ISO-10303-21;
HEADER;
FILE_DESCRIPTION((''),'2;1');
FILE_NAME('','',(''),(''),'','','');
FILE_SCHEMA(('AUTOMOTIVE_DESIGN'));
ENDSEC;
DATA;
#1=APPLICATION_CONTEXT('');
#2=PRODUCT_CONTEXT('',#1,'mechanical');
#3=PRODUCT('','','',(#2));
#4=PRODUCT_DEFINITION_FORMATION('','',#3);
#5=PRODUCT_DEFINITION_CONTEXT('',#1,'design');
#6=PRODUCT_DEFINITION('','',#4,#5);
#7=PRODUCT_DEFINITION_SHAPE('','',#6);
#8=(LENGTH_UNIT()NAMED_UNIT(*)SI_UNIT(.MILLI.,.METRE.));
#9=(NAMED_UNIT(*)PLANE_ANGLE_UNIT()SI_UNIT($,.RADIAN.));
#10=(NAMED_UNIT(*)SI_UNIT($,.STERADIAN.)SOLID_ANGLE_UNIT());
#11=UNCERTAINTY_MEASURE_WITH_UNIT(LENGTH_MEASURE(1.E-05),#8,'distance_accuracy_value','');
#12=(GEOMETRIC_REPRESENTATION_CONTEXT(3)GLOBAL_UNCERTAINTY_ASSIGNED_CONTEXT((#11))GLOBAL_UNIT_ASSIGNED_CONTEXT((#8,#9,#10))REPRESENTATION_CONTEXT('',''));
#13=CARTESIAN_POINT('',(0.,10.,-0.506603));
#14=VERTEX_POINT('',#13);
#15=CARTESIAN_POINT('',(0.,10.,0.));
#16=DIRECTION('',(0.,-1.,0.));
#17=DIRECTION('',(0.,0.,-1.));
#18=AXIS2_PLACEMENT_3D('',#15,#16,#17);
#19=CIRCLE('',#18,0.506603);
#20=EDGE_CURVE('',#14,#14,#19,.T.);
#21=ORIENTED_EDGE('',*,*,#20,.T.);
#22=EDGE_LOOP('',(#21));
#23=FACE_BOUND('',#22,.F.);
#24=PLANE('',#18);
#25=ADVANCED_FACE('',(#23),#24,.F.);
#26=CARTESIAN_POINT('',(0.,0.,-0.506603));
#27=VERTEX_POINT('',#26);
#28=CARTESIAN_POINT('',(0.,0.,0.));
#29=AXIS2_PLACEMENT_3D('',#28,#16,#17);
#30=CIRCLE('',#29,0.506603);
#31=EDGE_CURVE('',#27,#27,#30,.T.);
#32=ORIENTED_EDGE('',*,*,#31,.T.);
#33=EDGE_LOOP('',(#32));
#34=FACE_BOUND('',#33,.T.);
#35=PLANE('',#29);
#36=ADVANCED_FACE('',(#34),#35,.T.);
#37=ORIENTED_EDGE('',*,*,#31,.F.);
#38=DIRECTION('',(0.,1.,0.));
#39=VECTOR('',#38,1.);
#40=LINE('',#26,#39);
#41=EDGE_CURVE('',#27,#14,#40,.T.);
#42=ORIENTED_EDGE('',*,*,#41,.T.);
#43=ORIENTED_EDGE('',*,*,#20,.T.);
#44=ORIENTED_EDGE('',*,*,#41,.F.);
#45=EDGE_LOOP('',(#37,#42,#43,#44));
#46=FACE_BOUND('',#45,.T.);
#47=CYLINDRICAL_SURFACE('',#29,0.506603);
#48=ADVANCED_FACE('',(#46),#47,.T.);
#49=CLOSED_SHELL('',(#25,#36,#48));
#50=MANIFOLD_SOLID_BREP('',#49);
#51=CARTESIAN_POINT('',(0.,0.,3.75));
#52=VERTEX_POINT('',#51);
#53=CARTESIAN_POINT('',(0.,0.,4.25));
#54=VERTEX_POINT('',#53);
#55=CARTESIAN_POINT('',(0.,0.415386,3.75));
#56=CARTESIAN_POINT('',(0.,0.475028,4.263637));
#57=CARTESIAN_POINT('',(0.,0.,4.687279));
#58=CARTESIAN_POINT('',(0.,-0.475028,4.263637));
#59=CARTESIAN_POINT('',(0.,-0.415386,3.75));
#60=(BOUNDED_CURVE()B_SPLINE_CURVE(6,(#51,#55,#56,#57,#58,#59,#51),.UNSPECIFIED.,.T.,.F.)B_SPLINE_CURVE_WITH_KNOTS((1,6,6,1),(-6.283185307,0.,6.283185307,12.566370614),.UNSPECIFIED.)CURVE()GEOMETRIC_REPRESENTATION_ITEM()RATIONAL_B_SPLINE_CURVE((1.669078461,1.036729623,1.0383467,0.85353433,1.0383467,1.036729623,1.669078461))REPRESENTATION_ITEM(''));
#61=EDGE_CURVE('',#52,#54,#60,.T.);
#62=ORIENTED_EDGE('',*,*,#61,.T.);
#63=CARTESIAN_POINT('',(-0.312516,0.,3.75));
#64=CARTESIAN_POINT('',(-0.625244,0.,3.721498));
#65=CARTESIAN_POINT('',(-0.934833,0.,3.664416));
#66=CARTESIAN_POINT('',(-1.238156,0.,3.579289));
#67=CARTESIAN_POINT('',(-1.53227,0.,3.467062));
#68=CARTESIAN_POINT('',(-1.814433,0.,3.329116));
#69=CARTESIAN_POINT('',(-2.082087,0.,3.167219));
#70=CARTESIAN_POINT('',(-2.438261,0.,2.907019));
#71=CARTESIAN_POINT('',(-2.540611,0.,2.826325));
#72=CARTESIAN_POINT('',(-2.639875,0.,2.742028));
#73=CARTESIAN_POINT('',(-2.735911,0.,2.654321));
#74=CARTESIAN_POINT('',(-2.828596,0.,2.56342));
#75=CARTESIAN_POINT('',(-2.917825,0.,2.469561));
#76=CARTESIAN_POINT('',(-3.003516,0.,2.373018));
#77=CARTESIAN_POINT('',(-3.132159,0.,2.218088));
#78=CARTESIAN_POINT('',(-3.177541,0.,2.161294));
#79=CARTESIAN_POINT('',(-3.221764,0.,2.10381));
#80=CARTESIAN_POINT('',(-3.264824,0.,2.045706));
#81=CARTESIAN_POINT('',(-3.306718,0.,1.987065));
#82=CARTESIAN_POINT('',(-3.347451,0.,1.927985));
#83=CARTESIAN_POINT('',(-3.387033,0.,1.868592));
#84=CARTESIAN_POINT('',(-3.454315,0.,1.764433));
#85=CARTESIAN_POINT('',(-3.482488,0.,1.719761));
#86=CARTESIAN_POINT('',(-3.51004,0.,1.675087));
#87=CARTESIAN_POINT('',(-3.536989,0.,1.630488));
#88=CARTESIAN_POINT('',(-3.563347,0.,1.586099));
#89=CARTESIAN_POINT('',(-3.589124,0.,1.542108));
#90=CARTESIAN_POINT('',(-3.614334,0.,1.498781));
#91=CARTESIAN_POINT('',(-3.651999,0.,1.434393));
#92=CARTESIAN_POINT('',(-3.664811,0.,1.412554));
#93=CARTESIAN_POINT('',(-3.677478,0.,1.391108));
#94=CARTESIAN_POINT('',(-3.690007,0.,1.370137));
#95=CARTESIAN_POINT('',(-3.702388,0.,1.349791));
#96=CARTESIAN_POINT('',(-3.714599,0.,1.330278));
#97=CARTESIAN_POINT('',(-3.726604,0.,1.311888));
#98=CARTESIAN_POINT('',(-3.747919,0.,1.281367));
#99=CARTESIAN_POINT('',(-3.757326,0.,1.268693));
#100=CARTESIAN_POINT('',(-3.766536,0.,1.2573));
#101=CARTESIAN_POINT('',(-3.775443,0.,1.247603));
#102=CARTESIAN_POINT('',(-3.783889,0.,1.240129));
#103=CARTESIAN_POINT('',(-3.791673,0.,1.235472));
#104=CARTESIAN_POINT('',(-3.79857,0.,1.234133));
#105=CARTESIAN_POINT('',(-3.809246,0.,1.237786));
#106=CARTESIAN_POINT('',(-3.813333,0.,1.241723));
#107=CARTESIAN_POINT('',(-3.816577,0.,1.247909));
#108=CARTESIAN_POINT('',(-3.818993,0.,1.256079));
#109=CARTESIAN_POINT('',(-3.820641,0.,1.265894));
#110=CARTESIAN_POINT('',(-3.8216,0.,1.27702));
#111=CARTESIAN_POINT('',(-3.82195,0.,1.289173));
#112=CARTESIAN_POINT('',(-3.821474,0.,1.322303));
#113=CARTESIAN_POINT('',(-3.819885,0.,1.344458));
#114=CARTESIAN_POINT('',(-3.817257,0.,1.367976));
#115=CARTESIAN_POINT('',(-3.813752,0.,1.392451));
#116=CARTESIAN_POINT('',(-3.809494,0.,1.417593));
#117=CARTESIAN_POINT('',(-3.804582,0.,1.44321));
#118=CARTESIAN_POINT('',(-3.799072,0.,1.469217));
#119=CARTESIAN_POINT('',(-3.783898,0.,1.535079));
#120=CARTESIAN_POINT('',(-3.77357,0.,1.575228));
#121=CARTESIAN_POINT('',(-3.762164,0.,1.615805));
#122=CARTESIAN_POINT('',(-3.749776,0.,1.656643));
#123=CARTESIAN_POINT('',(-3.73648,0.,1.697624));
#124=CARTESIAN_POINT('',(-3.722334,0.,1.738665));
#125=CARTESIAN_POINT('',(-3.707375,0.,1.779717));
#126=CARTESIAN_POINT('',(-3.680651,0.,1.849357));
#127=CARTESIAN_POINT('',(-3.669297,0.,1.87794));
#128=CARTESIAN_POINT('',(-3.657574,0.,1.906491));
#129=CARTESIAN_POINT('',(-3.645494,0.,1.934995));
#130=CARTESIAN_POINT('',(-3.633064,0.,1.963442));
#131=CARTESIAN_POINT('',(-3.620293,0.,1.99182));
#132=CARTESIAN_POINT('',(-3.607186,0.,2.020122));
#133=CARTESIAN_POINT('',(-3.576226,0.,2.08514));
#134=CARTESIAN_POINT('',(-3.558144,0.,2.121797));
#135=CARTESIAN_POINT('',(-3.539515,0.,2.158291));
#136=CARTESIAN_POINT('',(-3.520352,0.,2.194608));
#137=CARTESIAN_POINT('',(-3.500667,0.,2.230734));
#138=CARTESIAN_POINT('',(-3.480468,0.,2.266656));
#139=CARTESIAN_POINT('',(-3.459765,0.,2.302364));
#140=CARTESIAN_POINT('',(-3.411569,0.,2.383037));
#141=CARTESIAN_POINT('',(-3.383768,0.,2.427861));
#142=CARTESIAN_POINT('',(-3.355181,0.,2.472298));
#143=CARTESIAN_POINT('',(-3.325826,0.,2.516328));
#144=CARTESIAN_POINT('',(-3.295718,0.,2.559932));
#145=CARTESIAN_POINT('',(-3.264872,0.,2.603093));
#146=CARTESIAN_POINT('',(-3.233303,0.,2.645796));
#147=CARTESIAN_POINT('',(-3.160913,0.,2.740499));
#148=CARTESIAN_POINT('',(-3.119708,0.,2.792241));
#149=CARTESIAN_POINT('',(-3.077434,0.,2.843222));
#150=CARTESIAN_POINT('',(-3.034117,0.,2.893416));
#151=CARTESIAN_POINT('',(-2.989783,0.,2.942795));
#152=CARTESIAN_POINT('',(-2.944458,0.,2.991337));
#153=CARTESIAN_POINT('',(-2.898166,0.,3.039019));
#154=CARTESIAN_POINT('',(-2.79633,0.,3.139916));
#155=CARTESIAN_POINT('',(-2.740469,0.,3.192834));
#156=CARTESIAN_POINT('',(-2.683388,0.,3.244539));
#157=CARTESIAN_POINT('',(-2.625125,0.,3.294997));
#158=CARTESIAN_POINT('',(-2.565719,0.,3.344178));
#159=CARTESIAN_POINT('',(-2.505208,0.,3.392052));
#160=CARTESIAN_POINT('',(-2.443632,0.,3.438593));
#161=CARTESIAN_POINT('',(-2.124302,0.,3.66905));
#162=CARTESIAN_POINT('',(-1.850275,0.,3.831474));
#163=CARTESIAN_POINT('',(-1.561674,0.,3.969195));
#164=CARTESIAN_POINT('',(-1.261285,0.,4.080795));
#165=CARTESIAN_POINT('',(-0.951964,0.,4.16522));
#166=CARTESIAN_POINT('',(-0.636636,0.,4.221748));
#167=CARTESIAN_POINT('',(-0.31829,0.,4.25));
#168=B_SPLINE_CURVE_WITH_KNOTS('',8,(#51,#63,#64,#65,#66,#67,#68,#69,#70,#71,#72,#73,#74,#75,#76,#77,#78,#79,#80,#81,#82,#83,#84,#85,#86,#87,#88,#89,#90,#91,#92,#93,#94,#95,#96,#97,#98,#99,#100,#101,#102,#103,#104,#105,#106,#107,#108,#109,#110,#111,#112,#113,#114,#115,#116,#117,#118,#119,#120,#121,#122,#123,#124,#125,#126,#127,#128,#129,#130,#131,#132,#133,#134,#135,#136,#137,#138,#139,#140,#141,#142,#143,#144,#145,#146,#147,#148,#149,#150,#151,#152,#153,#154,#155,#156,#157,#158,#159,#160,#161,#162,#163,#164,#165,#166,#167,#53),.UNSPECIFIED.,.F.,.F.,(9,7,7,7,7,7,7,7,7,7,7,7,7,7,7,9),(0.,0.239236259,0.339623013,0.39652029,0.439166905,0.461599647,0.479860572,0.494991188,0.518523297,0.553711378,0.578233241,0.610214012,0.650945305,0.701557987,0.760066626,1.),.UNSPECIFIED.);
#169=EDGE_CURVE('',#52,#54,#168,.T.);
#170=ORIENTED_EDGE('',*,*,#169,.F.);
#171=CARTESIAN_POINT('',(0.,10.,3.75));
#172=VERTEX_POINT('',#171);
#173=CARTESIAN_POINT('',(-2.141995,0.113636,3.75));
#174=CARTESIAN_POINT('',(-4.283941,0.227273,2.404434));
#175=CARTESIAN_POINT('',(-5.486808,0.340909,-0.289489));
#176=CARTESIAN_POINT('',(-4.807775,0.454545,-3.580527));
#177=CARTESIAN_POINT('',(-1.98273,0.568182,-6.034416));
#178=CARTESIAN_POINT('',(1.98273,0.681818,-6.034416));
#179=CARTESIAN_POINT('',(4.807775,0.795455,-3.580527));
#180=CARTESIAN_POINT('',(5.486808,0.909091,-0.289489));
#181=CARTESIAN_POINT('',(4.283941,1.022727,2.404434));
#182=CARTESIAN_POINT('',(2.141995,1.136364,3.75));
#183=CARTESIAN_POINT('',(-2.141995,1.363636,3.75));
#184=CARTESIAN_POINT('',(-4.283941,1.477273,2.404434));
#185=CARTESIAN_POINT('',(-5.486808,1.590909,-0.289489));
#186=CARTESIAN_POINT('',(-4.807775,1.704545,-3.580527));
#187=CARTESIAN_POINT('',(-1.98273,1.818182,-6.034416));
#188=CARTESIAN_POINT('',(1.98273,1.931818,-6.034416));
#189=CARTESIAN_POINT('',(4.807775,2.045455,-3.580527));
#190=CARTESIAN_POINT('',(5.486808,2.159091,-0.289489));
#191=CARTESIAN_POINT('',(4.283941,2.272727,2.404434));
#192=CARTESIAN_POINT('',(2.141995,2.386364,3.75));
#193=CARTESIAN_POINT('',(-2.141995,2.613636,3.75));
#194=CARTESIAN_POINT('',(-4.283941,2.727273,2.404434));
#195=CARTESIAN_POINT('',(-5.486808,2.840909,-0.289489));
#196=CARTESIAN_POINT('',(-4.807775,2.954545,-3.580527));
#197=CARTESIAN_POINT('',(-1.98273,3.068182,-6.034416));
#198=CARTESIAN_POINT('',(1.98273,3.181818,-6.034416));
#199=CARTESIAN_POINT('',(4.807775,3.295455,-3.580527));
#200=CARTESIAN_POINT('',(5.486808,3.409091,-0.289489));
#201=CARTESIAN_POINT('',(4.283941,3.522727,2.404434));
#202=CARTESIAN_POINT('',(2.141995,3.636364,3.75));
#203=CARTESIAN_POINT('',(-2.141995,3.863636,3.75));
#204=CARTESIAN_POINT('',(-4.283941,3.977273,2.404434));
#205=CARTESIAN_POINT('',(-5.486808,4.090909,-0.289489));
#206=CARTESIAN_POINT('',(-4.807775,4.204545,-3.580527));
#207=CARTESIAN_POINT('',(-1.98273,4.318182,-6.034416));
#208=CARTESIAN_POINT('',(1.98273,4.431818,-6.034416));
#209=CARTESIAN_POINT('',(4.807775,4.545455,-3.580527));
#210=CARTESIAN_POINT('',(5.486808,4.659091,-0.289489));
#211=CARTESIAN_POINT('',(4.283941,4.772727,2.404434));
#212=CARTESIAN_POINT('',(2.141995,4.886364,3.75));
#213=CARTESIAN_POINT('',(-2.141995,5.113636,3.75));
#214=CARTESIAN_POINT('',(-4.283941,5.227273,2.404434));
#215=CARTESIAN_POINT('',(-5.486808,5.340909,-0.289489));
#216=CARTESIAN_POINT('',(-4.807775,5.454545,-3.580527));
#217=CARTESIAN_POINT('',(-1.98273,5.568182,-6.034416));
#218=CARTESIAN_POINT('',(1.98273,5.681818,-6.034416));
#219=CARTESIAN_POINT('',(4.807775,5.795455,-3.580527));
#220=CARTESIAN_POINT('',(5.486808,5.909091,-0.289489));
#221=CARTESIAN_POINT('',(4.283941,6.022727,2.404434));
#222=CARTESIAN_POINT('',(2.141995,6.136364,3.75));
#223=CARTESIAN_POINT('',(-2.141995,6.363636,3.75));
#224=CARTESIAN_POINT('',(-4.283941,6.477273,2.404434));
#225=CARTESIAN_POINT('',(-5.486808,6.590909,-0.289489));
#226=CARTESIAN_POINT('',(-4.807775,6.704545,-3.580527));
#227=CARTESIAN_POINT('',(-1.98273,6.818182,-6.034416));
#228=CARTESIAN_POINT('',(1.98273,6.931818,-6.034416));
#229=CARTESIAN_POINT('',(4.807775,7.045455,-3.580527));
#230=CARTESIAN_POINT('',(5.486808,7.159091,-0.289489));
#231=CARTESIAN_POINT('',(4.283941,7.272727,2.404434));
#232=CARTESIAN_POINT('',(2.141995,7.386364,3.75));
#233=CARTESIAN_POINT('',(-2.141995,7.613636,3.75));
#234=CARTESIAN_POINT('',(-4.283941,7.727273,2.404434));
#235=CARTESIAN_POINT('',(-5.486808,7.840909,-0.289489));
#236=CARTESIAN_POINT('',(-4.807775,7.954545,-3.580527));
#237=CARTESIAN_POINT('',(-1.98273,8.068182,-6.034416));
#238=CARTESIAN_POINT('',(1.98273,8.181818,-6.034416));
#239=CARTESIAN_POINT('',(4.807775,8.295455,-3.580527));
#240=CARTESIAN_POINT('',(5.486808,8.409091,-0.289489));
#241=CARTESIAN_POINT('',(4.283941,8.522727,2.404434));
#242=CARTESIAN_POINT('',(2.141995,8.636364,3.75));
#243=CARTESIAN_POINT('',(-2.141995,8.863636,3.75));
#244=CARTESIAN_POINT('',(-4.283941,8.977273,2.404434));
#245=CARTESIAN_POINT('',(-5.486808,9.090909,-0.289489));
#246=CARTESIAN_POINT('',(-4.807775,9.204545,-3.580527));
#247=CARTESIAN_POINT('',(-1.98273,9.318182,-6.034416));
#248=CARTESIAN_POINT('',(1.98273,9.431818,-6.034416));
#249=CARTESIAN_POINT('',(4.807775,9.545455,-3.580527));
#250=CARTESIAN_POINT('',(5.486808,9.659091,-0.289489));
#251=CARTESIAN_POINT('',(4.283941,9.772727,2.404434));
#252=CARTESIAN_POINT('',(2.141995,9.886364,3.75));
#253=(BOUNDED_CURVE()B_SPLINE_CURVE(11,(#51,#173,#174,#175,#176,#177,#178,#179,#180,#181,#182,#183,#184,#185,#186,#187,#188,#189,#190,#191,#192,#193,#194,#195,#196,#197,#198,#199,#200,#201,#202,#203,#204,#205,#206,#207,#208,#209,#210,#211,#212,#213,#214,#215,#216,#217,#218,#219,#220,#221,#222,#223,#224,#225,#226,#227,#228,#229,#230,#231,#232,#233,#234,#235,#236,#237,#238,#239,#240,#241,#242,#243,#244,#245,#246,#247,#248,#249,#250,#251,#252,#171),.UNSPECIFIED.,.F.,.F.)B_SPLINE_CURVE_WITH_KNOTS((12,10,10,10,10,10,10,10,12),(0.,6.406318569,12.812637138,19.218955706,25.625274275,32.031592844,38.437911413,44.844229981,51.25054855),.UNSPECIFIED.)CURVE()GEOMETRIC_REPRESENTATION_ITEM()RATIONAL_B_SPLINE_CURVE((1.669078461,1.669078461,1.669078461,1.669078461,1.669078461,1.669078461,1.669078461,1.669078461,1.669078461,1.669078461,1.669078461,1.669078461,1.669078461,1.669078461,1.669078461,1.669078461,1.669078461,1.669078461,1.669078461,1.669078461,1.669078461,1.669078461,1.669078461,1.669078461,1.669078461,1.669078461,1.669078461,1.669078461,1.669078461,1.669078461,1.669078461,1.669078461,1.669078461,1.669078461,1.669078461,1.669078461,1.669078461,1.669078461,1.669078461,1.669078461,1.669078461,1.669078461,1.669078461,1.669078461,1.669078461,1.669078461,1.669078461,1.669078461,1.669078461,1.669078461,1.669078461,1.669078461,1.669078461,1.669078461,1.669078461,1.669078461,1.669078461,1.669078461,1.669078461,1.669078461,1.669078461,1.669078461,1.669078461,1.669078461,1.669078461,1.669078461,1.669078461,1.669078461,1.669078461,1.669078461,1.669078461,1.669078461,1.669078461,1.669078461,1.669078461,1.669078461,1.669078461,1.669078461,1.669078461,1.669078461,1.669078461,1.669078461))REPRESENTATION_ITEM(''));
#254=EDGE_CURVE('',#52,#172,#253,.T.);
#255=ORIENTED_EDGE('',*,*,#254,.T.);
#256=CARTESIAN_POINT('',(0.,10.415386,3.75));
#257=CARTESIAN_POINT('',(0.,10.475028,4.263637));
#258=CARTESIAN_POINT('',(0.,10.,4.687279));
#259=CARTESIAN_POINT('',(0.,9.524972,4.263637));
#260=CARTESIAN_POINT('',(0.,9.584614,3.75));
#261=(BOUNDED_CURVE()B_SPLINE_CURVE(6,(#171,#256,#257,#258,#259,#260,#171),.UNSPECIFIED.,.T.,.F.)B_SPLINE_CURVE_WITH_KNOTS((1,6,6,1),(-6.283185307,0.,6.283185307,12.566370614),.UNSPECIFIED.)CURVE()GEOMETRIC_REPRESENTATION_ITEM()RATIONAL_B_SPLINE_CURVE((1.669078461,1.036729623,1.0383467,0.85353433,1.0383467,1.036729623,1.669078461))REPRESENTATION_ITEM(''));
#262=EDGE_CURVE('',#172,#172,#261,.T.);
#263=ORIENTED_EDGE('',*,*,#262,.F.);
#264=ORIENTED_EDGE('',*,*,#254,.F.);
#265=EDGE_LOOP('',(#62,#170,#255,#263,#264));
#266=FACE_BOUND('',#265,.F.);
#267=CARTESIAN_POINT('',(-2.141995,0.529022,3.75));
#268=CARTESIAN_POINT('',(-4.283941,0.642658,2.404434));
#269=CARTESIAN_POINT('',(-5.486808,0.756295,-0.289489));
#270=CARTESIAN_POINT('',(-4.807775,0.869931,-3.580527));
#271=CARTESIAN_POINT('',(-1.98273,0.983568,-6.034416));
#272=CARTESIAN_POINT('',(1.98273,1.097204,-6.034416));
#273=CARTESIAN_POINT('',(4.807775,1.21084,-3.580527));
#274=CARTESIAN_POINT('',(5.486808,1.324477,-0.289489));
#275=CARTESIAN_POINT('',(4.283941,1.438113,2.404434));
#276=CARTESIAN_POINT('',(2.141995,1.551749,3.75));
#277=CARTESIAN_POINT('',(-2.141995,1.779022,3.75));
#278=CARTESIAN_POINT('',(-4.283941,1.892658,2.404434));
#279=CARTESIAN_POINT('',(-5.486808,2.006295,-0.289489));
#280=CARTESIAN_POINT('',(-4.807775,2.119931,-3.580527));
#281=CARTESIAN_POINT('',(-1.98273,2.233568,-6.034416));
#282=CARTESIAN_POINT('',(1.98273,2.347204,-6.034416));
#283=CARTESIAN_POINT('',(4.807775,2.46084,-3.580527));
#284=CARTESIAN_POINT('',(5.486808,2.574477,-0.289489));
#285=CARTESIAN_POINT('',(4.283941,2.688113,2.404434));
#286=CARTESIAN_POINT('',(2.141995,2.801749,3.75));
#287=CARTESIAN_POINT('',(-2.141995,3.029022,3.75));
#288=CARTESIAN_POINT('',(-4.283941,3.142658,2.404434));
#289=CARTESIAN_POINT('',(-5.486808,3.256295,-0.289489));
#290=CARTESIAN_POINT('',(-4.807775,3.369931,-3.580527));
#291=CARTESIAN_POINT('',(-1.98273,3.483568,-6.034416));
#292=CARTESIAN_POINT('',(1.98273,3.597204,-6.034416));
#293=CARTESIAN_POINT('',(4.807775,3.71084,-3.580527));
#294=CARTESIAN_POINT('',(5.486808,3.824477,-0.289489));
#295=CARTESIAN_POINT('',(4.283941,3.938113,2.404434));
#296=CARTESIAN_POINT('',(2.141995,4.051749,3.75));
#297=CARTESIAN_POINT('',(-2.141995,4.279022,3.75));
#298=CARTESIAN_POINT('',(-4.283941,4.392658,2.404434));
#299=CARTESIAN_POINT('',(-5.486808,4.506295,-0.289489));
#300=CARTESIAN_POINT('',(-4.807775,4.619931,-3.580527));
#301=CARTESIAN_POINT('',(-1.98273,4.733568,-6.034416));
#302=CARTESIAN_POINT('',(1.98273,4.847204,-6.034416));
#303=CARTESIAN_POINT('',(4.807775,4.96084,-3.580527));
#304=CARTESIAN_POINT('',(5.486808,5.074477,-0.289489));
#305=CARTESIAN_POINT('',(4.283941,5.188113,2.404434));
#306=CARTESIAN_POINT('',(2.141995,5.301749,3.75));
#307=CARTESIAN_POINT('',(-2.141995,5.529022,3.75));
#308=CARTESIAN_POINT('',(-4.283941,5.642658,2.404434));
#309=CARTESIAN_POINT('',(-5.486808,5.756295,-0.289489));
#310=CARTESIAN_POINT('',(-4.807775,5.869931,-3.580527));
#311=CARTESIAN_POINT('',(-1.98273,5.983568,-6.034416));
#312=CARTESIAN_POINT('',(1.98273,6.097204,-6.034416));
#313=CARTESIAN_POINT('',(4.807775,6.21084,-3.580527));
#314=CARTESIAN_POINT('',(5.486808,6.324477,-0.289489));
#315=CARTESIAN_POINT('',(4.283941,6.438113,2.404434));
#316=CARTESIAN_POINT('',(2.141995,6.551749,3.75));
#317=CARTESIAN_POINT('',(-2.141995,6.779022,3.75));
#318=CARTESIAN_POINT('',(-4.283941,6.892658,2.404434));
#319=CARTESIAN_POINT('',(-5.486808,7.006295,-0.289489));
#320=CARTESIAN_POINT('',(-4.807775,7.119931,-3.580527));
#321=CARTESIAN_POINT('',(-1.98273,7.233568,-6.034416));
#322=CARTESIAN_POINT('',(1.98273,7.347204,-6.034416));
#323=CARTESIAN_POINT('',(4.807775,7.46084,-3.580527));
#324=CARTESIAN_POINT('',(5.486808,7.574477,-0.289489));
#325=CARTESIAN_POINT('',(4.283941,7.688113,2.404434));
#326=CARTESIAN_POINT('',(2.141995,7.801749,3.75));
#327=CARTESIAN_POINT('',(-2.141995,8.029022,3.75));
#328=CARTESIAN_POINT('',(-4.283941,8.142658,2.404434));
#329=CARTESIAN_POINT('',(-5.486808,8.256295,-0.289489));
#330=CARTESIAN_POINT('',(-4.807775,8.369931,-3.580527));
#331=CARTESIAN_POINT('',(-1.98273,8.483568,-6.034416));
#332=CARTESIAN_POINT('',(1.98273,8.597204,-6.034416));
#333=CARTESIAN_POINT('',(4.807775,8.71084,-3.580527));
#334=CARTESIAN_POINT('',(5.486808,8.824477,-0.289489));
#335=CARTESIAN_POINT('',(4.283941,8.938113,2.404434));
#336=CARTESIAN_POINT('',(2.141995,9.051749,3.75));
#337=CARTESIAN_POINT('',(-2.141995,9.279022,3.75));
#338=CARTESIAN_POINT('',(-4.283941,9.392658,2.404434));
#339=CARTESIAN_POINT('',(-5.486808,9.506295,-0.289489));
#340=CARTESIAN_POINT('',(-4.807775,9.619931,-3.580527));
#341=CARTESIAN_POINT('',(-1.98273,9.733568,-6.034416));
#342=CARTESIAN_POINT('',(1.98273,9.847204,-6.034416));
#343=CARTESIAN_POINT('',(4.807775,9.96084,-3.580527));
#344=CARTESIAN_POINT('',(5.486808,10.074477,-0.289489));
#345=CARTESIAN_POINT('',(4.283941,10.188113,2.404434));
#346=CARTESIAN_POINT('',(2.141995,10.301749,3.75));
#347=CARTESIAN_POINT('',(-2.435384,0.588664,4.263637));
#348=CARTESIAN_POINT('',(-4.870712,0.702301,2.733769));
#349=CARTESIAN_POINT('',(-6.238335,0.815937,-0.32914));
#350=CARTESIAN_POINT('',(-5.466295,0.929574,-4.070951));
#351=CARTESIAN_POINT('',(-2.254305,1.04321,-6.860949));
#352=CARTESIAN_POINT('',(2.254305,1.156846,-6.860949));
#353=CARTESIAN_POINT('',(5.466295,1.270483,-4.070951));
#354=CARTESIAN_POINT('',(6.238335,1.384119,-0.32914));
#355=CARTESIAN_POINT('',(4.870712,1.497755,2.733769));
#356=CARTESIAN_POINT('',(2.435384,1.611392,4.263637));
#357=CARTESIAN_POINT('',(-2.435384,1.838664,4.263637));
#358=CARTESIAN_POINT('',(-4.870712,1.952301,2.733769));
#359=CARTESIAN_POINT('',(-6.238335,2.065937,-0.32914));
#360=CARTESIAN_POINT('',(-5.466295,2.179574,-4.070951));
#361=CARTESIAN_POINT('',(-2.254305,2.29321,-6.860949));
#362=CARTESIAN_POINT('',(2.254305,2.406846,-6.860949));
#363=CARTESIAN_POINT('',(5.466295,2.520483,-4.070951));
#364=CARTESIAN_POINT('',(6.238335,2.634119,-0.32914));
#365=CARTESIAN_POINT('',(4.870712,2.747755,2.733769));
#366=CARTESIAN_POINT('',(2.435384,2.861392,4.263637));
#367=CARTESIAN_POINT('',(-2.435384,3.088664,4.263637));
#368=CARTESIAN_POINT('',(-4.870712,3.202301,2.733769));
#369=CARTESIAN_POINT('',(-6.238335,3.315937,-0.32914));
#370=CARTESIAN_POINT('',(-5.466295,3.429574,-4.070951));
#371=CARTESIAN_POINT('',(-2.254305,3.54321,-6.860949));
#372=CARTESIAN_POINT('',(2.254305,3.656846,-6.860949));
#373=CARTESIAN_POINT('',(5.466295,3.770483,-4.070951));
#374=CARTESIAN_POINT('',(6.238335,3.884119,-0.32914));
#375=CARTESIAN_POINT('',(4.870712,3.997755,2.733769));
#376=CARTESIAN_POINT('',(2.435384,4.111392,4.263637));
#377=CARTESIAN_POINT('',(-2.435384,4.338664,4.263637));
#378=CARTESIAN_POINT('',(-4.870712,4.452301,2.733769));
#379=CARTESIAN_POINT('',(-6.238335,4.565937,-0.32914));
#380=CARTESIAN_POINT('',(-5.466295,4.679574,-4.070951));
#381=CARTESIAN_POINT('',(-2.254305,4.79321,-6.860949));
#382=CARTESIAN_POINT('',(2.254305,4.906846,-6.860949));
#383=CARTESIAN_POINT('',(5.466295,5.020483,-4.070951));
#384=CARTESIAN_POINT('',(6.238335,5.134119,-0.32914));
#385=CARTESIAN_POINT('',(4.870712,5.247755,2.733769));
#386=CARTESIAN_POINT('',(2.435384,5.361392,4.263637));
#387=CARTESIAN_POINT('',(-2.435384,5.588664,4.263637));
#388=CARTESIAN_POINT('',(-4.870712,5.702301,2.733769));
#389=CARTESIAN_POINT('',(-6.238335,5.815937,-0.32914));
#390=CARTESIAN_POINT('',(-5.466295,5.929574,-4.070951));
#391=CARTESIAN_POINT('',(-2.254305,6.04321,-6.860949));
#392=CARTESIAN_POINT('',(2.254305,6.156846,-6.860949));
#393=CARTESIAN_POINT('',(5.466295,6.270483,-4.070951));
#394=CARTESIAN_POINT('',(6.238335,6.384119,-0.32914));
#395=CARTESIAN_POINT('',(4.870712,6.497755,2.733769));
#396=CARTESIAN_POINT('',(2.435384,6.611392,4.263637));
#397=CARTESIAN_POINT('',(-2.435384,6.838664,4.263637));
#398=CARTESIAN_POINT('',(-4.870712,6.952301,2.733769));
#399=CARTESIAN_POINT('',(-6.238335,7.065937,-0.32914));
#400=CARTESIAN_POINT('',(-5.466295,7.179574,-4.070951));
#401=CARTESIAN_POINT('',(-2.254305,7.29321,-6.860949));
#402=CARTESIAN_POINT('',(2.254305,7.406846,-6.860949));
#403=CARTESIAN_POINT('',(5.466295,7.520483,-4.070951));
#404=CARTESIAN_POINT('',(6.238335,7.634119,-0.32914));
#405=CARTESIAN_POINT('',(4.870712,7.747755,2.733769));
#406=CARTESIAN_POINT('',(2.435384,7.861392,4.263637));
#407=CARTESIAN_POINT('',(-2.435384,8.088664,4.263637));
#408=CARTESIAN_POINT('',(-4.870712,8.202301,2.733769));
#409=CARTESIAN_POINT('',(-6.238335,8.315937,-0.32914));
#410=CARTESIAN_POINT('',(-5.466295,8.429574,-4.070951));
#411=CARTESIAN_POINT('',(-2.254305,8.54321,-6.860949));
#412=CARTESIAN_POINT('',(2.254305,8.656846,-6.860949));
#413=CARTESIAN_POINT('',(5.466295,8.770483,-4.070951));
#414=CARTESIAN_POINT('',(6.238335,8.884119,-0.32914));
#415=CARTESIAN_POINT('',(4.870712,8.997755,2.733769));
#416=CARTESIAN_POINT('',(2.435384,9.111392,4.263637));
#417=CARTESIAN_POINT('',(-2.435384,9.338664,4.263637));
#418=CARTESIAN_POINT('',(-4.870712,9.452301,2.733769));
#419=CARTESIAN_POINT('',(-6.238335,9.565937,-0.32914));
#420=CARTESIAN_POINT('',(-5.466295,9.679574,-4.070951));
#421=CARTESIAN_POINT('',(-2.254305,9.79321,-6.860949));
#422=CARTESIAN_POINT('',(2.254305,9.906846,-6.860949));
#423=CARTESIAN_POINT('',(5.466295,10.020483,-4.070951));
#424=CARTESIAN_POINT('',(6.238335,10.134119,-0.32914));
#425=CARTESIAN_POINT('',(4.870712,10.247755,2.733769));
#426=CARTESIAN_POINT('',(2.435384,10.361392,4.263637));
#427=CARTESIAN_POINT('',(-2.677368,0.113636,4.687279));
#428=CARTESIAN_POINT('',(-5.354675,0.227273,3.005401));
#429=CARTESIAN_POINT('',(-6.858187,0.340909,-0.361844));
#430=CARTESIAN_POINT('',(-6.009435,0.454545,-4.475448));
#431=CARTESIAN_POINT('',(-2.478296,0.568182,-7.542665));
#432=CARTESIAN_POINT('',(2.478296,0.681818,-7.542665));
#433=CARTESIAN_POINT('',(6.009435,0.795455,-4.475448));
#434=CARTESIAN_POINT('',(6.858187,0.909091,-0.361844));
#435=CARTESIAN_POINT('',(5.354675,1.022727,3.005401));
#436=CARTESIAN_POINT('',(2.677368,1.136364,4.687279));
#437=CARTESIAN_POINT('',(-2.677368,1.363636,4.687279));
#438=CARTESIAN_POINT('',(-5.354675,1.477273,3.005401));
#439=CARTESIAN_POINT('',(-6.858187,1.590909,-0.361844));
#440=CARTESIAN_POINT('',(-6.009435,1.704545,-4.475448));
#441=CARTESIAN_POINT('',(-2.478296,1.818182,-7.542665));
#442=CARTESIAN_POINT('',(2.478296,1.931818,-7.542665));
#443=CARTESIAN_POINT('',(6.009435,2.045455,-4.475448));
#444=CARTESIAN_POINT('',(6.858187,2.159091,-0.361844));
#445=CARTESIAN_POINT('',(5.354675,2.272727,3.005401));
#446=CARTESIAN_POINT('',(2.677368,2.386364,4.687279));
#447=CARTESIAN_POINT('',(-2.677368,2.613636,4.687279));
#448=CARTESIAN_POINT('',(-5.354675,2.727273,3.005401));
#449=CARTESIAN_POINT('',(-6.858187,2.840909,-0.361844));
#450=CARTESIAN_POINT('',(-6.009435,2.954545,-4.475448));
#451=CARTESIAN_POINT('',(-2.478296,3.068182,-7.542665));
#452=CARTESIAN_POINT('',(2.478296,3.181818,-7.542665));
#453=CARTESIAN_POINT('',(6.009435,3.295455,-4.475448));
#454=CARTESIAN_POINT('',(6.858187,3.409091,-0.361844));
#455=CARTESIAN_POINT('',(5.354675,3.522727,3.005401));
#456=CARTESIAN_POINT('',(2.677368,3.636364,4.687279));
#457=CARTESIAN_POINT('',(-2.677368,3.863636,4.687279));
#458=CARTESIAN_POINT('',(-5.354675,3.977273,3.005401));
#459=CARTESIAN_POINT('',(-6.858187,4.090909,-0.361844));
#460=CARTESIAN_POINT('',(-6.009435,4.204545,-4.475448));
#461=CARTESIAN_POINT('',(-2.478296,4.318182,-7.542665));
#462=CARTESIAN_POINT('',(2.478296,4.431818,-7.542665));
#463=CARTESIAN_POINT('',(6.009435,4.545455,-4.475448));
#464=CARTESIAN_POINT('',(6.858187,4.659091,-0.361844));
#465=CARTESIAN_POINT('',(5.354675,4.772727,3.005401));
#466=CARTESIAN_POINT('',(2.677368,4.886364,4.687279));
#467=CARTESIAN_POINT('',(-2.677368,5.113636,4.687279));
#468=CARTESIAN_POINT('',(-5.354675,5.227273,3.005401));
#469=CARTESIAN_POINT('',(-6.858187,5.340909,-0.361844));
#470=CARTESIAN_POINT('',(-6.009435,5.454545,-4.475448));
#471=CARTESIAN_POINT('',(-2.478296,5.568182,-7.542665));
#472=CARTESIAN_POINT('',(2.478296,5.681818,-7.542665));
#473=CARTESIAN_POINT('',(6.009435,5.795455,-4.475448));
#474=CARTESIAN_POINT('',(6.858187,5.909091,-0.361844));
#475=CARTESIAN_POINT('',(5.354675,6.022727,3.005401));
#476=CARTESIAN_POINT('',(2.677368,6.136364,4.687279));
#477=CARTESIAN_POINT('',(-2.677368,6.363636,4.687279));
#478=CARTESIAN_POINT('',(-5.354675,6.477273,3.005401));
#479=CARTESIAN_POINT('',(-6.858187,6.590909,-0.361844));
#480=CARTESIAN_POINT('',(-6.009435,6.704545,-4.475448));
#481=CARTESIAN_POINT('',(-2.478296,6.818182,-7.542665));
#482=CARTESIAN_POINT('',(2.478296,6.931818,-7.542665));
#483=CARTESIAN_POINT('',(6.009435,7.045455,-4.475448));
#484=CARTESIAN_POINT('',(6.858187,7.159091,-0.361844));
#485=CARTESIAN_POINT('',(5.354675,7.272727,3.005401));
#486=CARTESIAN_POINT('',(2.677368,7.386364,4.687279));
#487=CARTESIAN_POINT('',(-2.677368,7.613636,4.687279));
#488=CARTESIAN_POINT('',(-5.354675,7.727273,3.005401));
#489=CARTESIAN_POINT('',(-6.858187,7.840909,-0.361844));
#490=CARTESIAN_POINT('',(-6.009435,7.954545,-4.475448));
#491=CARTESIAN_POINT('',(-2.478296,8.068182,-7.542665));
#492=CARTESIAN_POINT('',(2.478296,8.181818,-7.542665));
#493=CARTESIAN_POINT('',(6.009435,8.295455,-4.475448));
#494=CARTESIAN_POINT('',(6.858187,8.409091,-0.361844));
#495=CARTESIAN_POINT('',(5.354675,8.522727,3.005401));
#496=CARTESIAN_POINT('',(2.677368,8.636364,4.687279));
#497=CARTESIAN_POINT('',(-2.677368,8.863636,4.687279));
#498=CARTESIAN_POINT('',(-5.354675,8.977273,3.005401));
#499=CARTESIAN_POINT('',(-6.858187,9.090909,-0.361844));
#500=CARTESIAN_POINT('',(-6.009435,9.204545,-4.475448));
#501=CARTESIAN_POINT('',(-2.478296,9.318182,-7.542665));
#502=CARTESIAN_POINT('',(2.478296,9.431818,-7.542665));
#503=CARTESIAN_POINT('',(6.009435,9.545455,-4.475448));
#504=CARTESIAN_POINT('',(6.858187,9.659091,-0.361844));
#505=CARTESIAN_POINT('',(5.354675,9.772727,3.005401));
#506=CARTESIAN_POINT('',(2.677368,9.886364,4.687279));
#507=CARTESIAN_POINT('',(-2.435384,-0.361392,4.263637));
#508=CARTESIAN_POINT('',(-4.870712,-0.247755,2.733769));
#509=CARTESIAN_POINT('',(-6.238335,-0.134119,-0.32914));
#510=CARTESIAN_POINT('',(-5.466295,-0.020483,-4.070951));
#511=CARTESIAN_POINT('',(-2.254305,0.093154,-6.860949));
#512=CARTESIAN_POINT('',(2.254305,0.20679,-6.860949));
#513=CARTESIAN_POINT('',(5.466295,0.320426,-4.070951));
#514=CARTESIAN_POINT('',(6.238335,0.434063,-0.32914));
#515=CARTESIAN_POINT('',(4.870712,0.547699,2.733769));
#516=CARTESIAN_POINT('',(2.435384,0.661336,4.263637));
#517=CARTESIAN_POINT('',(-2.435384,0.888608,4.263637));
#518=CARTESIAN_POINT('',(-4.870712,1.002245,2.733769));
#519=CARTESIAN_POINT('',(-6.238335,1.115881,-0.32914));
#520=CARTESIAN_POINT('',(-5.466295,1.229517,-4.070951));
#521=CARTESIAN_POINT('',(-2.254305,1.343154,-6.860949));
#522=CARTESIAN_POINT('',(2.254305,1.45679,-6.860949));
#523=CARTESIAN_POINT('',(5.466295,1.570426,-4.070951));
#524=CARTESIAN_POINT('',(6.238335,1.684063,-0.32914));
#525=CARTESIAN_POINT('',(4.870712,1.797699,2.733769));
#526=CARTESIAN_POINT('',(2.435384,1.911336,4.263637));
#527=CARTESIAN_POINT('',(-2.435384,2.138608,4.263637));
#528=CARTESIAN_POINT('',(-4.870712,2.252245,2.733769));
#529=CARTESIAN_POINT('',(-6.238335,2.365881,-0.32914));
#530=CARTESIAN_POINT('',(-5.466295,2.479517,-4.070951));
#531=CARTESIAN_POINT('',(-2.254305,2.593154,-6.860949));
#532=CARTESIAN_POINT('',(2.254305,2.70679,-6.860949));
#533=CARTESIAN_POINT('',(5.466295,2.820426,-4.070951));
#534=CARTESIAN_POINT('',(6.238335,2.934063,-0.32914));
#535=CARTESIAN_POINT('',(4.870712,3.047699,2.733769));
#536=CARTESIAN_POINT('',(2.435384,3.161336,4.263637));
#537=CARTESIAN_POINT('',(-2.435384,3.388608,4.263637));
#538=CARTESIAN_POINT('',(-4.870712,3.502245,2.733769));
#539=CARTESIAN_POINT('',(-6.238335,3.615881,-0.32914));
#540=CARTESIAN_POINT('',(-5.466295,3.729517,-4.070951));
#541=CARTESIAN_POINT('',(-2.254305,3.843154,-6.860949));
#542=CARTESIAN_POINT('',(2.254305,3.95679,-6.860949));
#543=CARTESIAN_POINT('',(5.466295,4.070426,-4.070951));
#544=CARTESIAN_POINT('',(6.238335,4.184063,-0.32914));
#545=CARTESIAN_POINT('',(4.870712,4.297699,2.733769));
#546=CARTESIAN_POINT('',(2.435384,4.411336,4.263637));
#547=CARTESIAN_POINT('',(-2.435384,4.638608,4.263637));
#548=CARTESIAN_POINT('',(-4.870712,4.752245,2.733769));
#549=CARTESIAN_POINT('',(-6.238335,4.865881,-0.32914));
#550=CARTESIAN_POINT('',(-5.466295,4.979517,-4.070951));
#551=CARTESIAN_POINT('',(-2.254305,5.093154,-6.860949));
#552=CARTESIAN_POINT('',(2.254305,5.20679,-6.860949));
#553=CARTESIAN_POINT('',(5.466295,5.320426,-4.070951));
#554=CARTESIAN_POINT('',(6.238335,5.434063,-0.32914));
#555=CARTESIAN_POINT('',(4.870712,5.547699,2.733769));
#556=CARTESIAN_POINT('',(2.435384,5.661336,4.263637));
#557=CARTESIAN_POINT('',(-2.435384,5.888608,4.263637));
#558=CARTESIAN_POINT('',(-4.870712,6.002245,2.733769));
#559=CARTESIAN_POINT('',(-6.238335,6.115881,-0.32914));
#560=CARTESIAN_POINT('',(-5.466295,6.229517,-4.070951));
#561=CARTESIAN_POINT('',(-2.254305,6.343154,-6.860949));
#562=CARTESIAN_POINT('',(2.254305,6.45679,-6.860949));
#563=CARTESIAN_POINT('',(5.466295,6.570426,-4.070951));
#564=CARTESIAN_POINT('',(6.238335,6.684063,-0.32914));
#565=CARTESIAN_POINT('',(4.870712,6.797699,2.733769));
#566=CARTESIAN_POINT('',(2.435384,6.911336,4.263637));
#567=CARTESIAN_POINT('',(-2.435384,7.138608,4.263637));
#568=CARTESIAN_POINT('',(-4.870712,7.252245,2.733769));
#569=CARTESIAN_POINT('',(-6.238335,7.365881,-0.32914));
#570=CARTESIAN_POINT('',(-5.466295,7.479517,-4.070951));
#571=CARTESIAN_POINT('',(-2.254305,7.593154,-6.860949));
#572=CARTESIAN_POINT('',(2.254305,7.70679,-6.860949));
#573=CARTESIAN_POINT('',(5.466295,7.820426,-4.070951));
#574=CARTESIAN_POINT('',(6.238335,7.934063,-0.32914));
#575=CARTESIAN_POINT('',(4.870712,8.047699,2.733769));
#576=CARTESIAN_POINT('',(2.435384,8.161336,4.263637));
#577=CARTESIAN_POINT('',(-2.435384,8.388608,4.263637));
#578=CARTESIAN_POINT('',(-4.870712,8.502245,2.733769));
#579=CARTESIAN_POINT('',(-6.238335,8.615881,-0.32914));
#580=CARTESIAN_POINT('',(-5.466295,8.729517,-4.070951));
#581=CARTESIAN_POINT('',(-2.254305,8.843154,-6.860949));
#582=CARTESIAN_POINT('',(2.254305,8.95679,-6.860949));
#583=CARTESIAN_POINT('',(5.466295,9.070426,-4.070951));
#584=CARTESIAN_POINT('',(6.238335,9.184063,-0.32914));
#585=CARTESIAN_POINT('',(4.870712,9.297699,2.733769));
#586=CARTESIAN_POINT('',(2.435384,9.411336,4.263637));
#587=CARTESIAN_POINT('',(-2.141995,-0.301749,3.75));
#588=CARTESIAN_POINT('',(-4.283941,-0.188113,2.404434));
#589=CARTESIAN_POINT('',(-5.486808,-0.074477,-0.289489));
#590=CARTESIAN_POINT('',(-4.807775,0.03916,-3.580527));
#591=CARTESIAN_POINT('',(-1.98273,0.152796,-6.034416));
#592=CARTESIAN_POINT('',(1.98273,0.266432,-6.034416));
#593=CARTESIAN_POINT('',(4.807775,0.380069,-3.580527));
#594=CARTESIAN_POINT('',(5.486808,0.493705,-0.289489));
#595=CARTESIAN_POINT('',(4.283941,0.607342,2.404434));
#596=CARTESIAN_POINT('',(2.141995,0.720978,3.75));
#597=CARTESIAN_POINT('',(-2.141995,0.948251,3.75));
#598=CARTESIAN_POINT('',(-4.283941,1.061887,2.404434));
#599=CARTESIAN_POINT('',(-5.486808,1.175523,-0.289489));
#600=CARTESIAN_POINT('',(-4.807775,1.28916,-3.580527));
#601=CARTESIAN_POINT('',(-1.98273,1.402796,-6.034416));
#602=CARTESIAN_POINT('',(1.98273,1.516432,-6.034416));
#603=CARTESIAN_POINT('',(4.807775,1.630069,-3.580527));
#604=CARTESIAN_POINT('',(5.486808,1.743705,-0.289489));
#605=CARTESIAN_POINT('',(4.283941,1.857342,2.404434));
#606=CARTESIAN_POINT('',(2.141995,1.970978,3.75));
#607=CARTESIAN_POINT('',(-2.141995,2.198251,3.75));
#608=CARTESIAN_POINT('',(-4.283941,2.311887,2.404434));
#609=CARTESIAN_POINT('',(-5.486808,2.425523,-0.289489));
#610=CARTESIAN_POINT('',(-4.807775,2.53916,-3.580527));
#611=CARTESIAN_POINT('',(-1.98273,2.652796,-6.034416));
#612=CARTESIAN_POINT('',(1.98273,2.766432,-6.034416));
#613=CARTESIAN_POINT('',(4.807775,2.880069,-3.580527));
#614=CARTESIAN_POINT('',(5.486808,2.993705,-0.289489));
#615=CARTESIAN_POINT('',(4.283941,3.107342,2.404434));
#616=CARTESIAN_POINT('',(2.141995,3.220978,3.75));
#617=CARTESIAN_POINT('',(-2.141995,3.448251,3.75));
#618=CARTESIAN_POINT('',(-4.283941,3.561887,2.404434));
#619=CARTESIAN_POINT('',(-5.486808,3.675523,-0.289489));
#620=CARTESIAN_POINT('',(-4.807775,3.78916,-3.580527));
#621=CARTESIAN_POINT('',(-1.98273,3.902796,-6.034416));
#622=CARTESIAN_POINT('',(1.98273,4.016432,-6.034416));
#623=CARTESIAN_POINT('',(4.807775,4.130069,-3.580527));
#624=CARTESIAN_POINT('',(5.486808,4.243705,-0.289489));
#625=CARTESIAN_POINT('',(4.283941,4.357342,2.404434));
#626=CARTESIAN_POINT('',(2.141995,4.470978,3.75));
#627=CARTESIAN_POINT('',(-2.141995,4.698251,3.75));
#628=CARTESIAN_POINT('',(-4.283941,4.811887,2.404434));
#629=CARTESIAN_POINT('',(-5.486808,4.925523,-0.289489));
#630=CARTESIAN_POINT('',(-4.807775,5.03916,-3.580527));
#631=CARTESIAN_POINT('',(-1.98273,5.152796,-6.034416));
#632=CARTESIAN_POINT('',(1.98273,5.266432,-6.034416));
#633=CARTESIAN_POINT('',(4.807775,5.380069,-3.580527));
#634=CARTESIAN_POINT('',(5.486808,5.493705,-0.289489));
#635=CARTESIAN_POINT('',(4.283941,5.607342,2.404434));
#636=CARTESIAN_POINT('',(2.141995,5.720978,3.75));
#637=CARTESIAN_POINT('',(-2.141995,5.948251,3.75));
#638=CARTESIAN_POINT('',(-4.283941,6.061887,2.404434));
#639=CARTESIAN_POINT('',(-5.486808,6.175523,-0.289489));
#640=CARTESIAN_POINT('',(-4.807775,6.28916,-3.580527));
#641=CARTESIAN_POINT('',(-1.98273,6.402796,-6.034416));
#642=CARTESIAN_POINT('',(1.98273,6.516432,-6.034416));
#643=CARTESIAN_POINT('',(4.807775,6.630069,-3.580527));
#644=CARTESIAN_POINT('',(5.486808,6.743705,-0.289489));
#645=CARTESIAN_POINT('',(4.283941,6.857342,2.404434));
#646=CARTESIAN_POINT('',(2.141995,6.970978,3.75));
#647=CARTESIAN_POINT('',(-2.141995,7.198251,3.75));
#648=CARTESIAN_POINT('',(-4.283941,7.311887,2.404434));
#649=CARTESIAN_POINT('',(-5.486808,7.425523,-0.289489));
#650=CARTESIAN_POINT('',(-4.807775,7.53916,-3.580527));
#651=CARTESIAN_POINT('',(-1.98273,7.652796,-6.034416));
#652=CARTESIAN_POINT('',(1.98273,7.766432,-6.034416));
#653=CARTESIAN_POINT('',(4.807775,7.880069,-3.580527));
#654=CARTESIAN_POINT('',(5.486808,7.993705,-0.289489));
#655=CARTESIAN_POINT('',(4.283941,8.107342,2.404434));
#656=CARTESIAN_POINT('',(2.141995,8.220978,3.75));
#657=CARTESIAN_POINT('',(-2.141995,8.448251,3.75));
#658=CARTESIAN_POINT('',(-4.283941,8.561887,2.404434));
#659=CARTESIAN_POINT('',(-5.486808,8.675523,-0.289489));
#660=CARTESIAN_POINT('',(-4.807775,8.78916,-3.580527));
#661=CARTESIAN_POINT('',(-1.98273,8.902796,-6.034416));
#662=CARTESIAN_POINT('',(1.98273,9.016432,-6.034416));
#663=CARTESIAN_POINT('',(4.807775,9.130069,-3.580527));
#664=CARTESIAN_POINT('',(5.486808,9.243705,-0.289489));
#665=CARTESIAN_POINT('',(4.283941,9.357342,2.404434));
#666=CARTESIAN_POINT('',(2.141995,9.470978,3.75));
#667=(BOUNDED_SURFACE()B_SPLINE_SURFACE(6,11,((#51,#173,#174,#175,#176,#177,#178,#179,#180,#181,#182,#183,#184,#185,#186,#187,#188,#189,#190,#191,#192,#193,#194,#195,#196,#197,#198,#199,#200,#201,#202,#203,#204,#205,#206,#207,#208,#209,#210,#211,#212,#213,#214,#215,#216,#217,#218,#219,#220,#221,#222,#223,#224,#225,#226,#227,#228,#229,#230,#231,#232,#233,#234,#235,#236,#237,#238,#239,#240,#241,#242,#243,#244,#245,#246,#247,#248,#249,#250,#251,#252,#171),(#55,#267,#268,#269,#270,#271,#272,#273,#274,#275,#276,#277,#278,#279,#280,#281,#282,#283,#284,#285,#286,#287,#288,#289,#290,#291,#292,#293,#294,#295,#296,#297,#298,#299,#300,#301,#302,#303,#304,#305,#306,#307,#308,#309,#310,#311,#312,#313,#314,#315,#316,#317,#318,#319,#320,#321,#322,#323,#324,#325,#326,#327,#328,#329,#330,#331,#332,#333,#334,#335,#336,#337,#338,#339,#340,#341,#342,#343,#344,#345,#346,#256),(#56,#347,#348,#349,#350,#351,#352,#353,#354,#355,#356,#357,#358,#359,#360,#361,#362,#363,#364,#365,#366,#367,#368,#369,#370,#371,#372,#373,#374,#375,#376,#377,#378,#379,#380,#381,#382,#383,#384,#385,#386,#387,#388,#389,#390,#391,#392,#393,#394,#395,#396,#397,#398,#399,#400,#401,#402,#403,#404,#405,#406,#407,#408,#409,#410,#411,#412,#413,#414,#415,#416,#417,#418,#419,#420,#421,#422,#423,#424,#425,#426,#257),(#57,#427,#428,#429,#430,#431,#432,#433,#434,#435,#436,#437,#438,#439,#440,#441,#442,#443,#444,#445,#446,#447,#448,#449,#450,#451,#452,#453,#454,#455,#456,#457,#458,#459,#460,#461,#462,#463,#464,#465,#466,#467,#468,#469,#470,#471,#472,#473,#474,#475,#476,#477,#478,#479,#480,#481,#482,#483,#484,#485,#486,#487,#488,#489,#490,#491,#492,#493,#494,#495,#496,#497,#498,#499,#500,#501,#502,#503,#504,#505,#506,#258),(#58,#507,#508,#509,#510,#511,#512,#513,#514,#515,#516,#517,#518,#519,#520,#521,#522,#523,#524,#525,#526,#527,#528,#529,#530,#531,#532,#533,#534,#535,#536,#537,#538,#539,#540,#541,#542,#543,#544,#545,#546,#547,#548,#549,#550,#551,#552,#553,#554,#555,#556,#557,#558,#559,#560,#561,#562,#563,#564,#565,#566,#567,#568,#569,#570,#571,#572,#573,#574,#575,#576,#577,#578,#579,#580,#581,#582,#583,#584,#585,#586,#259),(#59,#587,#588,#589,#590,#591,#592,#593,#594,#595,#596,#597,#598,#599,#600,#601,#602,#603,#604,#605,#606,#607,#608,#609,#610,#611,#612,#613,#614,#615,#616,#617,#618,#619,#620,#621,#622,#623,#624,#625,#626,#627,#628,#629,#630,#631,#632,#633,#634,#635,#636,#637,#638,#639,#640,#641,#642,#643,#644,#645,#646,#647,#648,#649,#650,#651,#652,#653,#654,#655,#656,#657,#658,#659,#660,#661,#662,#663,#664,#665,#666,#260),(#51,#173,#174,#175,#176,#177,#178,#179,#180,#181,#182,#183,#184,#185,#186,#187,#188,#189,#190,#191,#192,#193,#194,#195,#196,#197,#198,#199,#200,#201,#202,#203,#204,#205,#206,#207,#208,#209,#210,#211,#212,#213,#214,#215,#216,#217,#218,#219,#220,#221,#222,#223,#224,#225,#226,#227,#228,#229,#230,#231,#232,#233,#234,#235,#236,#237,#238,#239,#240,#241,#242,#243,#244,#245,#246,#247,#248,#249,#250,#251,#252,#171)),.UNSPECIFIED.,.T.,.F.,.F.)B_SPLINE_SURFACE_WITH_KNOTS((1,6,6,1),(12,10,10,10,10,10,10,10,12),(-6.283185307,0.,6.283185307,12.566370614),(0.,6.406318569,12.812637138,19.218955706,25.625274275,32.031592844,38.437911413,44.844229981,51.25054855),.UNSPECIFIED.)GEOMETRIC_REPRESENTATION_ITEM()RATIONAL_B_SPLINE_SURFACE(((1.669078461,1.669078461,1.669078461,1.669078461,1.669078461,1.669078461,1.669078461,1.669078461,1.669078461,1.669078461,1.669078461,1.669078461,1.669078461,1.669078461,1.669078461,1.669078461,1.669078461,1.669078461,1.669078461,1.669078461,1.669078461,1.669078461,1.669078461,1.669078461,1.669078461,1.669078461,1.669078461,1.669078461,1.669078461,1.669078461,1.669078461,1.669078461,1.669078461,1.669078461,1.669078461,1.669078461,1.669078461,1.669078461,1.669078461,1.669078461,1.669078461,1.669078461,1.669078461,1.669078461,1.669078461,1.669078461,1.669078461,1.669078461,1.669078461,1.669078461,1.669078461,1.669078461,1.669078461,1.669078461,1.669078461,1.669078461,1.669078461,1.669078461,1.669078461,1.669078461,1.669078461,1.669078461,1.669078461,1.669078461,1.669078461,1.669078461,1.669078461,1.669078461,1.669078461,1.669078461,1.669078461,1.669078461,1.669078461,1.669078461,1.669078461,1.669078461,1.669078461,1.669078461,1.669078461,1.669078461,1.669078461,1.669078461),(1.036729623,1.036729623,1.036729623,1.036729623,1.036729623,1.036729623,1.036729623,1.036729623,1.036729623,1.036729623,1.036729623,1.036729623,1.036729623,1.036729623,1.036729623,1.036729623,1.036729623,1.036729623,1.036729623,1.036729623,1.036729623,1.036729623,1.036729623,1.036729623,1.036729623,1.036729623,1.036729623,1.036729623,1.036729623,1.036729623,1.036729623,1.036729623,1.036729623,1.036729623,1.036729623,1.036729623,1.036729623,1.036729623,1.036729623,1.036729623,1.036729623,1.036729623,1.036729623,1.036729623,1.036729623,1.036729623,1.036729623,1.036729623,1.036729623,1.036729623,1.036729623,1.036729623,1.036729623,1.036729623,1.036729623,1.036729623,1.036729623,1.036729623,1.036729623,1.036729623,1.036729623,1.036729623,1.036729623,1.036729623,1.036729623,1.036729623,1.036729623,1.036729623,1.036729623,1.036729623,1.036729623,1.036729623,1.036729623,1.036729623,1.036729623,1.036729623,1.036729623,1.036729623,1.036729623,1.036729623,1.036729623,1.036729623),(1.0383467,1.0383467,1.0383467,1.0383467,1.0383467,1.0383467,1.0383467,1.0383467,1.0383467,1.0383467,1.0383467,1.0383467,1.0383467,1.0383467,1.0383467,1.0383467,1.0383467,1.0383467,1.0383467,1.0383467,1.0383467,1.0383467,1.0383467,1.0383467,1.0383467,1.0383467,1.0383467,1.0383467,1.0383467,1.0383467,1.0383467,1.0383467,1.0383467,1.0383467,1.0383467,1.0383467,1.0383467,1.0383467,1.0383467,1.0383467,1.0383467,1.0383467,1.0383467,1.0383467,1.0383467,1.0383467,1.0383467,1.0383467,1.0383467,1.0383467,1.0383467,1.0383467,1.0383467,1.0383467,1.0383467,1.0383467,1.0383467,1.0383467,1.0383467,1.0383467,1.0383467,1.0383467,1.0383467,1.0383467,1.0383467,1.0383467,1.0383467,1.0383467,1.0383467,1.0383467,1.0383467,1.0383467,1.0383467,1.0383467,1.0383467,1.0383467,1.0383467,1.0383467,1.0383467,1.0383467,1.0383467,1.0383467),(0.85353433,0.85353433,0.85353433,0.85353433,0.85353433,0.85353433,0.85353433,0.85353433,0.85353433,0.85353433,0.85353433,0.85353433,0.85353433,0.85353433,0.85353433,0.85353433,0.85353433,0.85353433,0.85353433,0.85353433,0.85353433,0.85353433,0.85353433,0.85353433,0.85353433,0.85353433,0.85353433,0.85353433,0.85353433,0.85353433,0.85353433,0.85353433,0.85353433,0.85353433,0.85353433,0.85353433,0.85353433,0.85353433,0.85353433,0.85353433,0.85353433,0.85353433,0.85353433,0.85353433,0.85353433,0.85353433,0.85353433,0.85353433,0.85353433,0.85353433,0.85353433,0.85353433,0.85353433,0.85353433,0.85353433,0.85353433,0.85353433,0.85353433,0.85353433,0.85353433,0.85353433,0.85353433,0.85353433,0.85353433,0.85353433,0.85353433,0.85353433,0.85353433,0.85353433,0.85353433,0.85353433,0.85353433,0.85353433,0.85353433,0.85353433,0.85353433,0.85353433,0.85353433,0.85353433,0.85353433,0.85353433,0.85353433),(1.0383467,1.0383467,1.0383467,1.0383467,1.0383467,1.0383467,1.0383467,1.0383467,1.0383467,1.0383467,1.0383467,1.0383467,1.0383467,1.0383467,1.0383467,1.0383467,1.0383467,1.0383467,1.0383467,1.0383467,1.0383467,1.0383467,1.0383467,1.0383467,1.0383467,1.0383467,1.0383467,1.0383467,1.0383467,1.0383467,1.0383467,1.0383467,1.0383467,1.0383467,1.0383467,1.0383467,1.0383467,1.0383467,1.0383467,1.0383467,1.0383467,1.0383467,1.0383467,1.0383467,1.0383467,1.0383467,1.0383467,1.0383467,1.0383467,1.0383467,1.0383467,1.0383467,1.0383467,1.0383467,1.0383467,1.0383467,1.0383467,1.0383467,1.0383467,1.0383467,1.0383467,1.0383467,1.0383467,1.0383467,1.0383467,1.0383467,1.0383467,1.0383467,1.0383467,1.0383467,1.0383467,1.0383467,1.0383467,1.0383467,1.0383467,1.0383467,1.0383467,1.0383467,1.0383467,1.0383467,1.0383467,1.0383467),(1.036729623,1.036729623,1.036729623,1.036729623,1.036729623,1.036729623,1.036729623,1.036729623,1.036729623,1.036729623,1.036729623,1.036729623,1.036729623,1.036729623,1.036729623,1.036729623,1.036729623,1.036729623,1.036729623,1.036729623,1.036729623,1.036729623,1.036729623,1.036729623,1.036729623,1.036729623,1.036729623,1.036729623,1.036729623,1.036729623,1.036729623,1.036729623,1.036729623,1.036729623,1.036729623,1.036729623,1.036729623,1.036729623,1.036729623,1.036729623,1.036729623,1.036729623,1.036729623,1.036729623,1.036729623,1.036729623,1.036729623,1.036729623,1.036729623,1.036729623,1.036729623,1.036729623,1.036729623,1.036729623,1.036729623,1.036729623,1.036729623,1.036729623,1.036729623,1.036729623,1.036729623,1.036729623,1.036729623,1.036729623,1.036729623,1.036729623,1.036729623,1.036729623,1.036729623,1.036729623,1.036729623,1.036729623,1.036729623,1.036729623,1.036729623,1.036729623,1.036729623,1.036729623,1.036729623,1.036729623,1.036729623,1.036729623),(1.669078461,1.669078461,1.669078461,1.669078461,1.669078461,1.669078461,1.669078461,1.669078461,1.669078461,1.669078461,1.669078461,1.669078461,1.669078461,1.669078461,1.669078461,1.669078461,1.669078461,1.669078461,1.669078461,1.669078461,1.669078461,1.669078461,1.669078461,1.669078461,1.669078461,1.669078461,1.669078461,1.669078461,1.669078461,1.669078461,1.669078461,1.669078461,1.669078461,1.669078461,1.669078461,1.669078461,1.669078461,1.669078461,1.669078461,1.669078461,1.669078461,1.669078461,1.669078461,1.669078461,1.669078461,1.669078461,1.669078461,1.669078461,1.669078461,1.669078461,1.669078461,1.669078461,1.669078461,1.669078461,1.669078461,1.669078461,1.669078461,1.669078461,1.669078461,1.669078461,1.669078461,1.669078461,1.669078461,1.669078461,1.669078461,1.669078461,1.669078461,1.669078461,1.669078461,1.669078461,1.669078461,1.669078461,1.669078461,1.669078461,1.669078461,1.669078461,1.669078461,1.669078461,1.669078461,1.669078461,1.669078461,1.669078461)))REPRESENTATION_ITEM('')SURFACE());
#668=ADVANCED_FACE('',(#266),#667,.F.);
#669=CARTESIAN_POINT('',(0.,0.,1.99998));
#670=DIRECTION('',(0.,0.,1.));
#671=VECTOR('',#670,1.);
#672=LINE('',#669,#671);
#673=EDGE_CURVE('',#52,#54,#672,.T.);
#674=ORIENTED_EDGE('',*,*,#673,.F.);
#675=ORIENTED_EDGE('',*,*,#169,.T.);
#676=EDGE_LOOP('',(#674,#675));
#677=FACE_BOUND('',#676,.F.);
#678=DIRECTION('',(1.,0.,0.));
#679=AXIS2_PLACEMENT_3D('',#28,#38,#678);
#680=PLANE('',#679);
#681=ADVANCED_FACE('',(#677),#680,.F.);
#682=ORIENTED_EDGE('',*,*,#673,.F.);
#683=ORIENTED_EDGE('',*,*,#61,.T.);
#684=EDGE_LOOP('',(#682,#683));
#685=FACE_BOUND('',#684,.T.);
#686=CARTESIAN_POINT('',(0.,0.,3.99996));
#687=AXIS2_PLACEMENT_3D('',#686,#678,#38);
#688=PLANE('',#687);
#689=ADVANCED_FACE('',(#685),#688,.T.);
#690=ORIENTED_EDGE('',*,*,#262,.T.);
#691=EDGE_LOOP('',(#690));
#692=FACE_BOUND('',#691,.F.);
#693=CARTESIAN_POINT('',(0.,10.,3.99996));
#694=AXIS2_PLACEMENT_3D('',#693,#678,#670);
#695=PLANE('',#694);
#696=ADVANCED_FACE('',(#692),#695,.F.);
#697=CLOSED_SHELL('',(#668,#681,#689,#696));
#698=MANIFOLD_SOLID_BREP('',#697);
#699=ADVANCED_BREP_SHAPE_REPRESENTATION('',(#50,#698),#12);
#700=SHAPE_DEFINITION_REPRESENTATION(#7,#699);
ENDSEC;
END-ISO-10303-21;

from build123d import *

# Parameters (mm, degrees)
SWEEP_1_PITCH       = 1.25
SWEEP_1_HEIGHT      = 10
SWEEP_1_RADIUS      = 4
SKETCH_3_R          = 0.25
SKETCH_4_R          = 5.626020109
CUT_EXTRUDE_1_DEPTH = 10
SKETCH_5_R          = 0.506602862
EXTRUDE_1_DEPTH     = 10


with BuildPart() as part:
    # 扫描1: sweep along a helix
    with BuildLine() as sweep_1_path:
        Helix(SWEEP_1_PITCH, SWEEP_1_HEIGHT, SWEEP_1_RADIUS, center=(0, 0, 0), direction=(0, 1, 0), lefthand=True)
    # 草图3 → 扫描1 (sweep)
    with BuildSketch(Plane(origin=(0, 0, 0), x_dir=(0, 0, -1), z_dir=(1, 0, 0))):
        with Locations((-4, 0)):
            Circle(SKETCH_3_R)
    sweep(path=sweep_1_path.line, is_frenet=True)

    # 草图4 → 切除-拉伸1 (cut)
    with BuildSketch(Plane(origin=(0, 0, 0), x_dir=(1, 0, 0), z_dir=(0, 1, 0))):
        Circle(SKETCH_4_R)
    extrude(amount=-CUT_EXTRUDE_1_DEPTH, mode=Mode.SUBTRACT)


with BuildPart() as body_2:
    # 草图5 → 凸台-拉伸1 (new body)
    with BuildSketch(Plane.XZ):
        with Locations(Location((0, 0, 0), (0, 0, 270))):
            Circle(SKETCH_5_R)
    extrude(amount=-EXTRUDE_1_DEPTH)


solid = Compound([part.part, body_2.part])
